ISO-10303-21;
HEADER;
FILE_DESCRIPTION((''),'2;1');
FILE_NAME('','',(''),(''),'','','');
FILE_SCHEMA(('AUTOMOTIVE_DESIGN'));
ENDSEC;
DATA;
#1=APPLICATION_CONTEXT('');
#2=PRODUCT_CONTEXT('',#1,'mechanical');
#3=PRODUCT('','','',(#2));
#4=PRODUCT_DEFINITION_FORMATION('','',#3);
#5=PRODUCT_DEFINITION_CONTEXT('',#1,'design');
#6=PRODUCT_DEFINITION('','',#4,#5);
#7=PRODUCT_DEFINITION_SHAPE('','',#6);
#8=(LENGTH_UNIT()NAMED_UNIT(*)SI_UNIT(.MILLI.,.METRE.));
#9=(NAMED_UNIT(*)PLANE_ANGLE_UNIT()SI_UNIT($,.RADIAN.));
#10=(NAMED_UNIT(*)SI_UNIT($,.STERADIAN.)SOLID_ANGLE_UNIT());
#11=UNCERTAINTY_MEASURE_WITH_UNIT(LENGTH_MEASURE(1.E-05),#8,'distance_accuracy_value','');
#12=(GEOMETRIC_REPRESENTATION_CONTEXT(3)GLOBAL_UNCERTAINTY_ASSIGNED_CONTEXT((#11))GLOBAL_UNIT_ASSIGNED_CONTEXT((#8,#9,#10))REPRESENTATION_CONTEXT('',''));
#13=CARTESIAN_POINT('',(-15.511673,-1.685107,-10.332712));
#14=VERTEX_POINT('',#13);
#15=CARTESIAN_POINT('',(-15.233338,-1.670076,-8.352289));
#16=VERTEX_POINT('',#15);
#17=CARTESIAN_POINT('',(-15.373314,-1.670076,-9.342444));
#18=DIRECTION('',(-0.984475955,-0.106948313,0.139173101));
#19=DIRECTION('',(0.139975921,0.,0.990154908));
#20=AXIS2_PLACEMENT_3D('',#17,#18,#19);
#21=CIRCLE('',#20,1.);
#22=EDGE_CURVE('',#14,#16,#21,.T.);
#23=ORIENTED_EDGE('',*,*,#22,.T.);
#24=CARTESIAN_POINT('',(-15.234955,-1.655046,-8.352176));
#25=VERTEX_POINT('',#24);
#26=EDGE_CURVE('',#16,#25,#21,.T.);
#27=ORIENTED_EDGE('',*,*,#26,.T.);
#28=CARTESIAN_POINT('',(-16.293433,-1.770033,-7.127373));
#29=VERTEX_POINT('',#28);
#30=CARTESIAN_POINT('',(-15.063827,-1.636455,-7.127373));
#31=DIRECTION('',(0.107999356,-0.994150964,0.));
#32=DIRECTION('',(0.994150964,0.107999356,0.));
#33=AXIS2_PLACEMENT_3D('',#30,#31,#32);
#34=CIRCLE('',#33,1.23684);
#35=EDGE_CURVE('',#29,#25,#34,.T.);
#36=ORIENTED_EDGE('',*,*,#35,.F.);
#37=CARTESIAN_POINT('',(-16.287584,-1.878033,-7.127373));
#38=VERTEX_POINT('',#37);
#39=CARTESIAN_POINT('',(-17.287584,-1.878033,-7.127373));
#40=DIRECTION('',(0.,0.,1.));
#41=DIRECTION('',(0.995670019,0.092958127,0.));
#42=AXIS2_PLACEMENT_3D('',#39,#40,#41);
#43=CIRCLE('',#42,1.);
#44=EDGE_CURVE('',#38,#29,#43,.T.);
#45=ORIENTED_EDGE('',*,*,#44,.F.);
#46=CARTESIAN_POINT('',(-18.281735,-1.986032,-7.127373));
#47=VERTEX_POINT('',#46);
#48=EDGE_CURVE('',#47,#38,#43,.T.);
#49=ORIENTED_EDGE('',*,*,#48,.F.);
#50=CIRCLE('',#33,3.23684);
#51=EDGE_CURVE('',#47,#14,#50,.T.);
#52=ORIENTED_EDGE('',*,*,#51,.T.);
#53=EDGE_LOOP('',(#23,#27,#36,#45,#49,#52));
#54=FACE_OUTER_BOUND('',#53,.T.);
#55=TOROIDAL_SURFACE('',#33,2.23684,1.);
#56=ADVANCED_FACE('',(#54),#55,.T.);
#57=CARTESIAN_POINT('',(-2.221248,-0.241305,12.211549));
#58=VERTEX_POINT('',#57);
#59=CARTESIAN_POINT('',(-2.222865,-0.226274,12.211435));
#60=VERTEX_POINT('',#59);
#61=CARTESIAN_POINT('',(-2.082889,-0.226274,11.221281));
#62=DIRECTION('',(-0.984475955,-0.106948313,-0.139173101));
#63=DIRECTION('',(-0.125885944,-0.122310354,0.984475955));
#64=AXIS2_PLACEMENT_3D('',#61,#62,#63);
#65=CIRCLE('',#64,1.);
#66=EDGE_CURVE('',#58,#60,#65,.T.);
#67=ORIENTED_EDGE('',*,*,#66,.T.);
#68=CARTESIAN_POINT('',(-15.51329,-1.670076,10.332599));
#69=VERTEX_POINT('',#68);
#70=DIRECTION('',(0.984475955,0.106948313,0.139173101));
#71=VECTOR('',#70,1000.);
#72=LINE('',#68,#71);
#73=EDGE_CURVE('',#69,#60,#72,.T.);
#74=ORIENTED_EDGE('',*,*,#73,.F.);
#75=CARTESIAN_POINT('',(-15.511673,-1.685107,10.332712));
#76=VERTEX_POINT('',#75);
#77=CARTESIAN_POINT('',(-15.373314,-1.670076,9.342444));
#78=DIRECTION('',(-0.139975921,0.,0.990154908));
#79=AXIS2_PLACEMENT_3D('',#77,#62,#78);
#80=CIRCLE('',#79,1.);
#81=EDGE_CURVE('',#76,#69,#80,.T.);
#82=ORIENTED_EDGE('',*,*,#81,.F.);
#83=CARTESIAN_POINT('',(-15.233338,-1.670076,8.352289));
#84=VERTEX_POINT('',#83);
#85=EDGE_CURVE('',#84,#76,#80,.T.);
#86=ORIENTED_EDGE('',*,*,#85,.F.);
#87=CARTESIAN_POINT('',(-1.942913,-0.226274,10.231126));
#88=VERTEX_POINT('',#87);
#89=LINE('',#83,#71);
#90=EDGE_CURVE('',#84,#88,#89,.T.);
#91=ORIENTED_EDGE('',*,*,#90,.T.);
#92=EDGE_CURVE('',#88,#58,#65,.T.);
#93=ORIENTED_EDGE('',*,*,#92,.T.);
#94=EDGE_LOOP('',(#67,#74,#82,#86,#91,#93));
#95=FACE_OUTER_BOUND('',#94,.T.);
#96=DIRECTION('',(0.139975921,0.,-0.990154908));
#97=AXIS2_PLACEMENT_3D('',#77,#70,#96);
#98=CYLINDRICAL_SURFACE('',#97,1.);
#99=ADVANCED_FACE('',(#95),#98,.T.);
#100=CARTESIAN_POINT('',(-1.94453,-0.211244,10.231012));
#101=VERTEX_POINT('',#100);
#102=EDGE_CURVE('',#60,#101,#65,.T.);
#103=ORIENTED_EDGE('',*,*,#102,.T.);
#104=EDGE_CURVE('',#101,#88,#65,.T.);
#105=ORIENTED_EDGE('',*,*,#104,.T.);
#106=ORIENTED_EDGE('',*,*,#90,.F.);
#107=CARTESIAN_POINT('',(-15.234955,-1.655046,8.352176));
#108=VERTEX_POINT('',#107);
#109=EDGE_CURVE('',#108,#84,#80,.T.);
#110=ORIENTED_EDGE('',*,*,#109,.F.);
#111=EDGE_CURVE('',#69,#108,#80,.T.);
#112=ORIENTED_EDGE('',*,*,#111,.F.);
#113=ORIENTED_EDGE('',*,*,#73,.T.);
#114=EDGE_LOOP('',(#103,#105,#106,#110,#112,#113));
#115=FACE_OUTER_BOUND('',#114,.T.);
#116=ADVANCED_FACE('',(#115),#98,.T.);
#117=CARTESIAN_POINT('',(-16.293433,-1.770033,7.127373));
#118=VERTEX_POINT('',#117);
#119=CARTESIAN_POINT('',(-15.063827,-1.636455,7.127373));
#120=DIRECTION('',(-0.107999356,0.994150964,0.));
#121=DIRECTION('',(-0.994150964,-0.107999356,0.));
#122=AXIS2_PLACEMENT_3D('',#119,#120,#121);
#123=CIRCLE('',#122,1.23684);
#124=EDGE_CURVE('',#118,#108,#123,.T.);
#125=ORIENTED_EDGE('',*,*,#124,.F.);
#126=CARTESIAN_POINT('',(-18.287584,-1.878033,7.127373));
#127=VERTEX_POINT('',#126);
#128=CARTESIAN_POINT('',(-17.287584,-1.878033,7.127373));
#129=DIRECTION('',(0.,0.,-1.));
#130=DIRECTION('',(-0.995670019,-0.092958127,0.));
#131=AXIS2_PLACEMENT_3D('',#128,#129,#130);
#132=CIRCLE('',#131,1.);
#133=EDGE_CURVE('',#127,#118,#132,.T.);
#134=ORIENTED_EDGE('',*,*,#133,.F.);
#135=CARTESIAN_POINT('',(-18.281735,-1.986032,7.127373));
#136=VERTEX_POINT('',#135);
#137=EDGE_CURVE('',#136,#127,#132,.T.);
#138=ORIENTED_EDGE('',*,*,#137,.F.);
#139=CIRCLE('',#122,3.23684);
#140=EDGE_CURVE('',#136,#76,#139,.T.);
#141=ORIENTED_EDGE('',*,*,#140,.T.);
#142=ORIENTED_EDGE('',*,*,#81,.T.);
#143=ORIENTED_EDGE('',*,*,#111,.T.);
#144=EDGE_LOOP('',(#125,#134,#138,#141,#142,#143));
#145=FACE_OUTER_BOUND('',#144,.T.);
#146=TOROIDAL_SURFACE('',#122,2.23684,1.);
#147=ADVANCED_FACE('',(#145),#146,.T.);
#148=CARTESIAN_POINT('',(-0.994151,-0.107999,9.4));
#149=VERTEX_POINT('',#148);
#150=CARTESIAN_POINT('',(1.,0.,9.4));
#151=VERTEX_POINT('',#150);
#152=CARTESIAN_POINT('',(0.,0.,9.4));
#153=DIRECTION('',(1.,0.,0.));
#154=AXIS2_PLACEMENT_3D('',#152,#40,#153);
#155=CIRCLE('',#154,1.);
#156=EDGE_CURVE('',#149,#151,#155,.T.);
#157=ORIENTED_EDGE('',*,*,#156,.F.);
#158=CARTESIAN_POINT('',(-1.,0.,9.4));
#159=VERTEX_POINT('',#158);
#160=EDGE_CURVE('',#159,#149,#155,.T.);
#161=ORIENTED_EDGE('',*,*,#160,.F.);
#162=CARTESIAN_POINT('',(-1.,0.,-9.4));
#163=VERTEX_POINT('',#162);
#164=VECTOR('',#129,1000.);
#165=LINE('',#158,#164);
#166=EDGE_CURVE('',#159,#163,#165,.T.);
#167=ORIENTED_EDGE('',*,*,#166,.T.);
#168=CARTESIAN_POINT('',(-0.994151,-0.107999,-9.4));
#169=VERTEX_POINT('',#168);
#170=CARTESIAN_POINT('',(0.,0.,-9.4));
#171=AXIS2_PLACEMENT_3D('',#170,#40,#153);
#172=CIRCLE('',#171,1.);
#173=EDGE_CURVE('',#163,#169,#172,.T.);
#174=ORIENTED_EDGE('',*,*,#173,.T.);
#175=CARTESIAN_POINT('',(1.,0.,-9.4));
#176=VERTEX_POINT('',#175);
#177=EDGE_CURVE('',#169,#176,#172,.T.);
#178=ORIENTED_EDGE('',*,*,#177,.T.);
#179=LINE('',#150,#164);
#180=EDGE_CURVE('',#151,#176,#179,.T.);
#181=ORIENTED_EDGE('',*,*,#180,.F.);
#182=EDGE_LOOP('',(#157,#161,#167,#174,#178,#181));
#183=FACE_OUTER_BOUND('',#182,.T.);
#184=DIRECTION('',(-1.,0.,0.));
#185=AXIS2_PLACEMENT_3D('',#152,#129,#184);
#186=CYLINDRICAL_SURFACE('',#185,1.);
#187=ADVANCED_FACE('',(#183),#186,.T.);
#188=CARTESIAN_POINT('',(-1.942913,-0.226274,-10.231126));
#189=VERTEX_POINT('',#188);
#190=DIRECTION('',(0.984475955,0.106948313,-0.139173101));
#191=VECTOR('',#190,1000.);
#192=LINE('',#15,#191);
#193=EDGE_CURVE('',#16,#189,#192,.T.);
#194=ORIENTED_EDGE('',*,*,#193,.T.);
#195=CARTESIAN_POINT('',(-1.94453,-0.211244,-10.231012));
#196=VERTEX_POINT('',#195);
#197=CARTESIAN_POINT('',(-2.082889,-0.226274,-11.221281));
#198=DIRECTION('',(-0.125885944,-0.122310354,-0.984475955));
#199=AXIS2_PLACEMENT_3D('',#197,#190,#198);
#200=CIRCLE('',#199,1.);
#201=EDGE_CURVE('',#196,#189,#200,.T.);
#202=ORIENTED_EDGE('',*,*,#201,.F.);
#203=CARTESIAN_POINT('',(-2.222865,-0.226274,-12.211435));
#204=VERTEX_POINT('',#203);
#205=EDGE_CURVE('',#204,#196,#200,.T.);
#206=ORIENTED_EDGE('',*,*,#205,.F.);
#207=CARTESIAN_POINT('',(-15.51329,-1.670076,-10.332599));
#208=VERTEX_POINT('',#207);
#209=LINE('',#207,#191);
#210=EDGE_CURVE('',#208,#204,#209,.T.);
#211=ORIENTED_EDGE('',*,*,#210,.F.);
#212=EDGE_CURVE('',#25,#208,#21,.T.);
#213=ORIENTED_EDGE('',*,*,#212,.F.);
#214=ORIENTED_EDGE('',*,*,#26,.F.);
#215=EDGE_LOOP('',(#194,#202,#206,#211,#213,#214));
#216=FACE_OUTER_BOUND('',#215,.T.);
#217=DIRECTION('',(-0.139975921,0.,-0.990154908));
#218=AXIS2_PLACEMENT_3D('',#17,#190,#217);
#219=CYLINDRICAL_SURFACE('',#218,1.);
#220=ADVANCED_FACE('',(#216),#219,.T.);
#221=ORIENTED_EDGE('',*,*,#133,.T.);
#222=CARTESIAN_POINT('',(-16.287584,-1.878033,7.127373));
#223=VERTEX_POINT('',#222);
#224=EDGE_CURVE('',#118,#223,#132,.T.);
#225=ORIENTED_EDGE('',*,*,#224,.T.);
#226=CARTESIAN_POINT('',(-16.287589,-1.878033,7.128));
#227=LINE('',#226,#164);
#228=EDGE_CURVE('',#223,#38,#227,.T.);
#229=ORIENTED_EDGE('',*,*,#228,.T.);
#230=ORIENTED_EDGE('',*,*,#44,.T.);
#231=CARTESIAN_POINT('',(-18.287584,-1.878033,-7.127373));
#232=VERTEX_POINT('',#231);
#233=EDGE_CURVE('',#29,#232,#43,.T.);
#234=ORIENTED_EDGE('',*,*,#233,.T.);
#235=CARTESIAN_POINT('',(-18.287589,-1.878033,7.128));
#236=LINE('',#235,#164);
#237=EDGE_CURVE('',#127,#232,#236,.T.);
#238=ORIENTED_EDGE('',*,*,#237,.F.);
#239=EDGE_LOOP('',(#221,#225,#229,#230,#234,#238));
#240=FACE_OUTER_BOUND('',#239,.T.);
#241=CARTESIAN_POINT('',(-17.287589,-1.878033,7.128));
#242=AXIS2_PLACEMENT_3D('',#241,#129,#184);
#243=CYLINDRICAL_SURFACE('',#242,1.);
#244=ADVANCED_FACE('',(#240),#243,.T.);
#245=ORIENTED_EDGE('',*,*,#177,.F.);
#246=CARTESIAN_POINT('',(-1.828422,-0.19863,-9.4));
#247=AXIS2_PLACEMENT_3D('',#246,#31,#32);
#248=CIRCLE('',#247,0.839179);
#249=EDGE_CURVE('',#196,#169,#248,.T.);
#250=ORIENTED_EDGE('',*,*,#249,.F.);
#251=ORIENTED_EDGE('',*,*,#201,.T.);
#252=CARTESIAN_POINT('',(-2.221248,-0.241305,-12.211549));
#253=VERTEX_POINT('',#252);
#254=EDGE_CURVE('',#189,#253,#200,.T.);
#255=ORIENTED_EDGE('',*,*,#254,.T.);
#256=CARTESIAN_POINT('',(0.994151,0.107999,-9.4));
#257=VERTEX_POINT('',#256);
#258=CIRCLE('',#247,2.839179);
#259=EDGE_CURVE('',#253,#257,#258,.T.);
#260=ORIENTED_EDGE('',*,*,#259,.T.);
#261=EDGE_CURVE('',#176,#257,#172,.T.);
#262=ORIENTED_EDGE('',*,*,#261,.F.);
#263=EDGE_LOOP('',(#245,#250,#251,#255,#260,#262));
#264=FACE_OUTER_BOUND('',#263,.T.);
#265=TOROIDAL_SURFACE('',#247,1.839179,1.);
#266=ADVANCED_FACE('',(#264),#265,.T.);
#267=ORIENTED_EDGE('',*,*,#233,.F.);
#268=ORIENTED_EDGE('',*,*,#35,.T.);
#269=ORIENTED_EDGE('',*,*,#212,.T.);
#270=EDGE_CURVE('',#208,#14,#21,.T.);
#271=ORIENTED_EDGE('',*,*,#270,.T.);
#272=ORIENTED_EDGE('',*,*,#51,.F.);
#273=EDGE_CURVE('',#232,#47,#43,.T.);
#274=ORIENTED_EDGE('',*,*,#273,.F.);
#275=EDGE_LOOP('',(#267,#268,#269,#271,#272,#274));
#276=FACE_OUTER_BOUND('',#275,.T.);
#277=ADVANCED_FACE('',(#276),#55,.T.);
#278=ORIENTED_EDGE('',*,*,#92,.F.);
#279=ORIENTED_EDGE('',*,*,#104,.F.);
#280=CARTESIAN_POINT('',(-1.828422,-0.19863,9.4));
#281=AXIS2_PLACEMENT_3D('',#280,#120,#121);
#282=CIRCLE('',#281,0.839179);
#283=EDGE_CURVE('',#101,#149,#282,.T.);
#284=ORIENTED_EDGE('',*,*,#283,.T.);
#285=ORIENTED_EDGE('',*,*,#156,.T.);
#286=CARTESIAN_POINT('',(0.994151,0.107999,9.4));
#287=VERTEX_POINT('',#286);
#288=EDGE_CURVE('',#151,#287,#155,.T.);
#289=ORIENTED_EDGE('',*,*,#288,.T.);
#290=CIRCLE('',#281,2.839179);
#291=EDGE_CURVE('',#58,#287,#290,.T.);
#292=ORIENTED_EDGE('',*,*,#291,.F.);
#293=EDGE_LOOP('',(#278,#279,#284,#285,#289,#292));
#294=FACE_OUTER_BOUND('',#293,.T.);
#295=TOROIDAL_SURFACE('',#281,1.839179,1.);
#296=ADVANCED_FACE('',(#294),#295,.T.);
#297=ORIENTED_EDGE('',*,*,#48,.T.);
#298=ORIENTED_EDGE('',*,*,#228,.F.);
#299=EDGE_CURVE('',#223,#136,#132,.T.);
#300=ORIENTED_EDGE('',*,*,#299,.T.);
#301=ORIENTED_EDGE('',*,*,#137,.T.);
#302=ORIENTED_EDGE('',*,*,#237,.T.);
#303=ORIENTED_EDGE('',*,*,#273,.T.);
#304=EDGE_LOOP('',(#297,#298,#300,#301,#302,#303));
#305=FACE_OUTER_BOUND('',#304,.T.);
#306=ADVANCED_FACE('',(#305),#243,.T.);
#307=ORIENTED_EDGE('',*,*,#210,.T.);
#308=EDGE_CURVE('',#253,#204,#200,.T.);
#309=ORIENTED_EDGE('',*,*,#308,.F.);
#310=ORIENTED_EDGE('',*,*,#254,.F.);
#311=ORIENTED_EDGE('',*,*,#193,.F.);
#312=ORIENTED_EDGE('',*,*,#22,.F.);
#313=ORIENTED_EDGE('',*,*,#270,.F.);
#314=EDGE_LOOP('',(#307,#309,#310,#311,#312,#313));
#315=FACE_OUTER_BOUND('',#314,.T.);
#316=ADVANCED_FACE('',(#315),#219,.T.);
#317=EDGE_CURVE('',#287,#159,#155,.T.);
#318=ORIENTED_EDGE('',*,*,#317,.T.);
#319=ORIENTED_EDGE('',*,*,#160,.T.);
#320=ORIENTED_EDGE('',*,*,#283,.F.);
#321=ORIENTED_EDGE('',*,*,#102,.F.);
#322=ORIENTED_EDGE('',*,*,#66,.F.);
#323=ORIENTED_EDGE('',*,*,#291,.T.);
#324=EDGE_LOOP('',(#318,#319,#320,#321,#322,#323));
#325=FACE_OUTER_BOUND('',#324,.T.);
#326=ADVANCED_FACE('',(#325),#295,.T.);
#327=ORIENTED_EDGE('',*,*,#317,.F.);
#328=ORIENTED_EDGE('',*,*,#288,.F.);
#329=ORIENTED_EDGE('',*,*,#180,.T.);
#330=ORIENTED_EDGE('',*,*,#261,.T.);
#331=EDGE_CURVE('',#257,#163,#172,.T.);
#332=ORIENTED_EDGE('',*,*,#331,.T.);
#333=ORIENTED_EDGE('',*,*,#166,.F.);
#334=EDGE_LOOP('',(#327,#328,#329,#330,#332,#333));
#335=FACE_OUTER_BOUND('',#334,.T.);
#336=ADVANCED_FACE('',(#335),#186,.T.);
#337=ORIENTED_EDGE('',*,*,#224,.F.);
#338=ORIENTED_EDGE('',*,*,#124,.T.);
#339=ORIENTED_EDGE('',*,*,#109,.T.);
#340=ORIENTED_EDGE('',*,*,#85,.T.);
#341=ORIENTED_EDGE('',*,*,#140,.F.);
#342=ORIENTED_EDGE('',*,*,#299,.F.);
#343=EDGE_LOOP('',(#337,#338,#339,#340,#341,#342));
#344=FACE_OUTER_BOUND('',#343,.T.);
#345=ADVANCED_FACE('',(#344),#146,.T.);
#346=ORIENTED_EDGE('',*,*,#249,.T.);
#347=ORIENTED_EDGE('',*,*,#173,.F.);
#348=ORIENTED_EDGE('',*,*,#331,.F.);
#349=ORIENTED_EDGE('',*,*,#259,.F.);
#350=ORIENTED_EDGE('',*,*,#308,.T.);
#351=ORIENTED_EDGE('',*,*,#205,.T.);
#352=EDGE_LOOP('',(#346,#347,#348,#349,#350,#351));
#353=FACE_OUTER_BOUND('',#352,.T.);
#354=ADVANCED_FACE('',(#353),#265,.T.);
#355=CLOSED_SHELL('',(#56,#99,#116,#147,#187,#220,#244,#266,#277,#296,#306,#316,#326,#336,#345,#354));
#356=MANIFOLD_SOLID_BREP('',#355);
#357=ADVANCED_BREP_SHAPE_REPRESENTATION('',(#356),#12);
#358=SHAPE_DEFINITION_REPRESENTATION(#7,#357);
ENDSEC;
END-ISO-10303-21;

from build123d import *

# Parameters (mm, degrees)
BOSS_EXTRUDE1_DEPTH      = 9.4
BOSS_EXTRUDE1_DEPTH_BACK = 9.4
SKETCH1_R                = 1
SKETCH2_R                = 1
REVOLVE1_ANGLE           = 98
SKETCH3_R                = 1
BOSS_EXTRUDE2_DEPTH      = 13.5
SKETCH5_R                = 1
REVOLVE2_ANGLE           = 98
SKETCH6_R                = 1
BOSS_EXTRUDE3_DEPTH      = 13.5
SKETCH7_R                = 1
REVOLVE3_ANGLE           = 82
SKETCH8_R                = 1
REVOLVE4_ANGLE           = 82
BOSS_EXTRUDE4_DEPTH      = 7.128
BOSS_EXTRUDE4_DEPTH_BACK = 7.128
SKETCH4_R                = 1


with BuildPart() as part:
    # Sketch1 → Boss-Extrude1 (new, two sides: drawn at the far end of the back side and taken through both)
    with BuildSketch(Plane.XY.offset(-BOSS_EXTRUDE1_DEPTH_BACK)):
        Circle(SKETCH1_R)
    extrude(amount=BOSS_EXTRUDE1_DEPTH + BOSS_EXTRUDE1_DEPTH_BACK)

    # Sketch2 → Revolve1 (revolve)
    with BuildSketch(Plane.XY.offset(-9.4)):
        with Locations(Location((0, 0, 0), (0, 0, 6.2))):
            Circle(SKETCH2_R)
    revolve(axis=Axis((-1.634001289, -1.988301928, -9.4), (-0.10799935570602286, 0.9941509639723154, 0)), revolution_arc=REVOLVE1_ANGLE)

    # Sketch3 → Boss-Extrude2 (add)
    with BuildSketch(Plane(origin=(-0.505088704, -0.054870192, 0.071403228), x_dir=(0.13835907247846538, 0.015030605235296325, 0.9902680687415704), z_dir=(-0.9844759551304353, -0.10694831340033709, 0.1391731009600654))):
        with Locations(Location((-11.403663414, 0, 0), (0, 0, 180))):
            Circle(SKETCH3_R)
    extrude(amount=BOSS_EXTRUDE2_DEPTH)

    # Sketch5 → Revolve2 (revolve)
    with BuildSketch(Plane.XY.offset(9.4)):
        with Locations(Location((0, 0, 0), (0, 0, 6.2))):
            Circle(SKETCH5_R)
    revolve(axis=Axis((-1.634001289, -1.988301928, 9.4), (0.10799935570602286, -0.9941509639723154, 0)), revolution_arc=REVOLVE2_ANGLE)

    # Sketch6 → Boss-Extrude3 (add)
    with BuildSketch(Plane(origin=(-0.505088704, -0.054870192, -0.071403228), x_dir=(-0.13835907247846538, -0.015030605235296325, 0.9902680687415704), z_dir=(-0.9844759551304353, -0.10694831340033709, -0.1391731009600654))):
        with Locations((11.403663414, 0)):
            Circle(SKETCH6_R)
    extrude(amount=BOSS_EXTRUDE3_DEPTH)

    # Sketch7 → Revolve3 (revolve)
    with BuildSketch(Plane(origin=(-13.795514099, -1.498672423, 1.950240091), x_dir=(0.13835907247846538, 0.015030605235296325, 0.9902680687415704), z_dir=(-0.9844759551304353, -0.10694831340033709, 0.1391731009600654))):
        with Locations(Location((-11.403663414, 0, 0), (0, 0, 180))):
            Circle(SKETCH7_R)
    revolve(axis=Axis((-20.490038802, 48.312670109, -7.127372755), (-0.10799935570602279, 0.9941509639723154, 0)), revolution_arc=REVOLVE3_ANGLE)

    # Sketch8 → Revolve4 (revolve)
    with BuildSketch(Plane(origin=(-13.795514099, -1.498672423, -1.950240091), x_dir=(-0.13835907247846538, -0.015030605235296325, 0.9902680687415704), z_dir=(-0.9844759551304353, -0.10694831340033709, -0.1391731009600654))):
        with Locations((11.403663414, 0)):
            Circle(SKETCH8_R)
    revolve(axis=Axis((-9.690103231, -51.102426288, 7.127372755), (0.10799935570602279, -0.9941509639723154, 0)), revolution_arc=REVOLVE4_ANGLE)

    # Sketch4 → Boss-Extrude4 (add, two sides: drawn at the far end of the back side and taken through both)
    with BuildSketch(Plane.XY.offset(-BOSS_EXTRUDE4_DEPTH_BACK)):
        with Locations(Location((-17.287589358, -1.878033196, 0), (0, 0, 186.2))):
            Circle(SKETCH4_R)
    extrude(amount=BOSS_EXTRUDE4_DEPTH + BOSS_EXTRUDE4_DEPTH_BACK)


solid = part.part
